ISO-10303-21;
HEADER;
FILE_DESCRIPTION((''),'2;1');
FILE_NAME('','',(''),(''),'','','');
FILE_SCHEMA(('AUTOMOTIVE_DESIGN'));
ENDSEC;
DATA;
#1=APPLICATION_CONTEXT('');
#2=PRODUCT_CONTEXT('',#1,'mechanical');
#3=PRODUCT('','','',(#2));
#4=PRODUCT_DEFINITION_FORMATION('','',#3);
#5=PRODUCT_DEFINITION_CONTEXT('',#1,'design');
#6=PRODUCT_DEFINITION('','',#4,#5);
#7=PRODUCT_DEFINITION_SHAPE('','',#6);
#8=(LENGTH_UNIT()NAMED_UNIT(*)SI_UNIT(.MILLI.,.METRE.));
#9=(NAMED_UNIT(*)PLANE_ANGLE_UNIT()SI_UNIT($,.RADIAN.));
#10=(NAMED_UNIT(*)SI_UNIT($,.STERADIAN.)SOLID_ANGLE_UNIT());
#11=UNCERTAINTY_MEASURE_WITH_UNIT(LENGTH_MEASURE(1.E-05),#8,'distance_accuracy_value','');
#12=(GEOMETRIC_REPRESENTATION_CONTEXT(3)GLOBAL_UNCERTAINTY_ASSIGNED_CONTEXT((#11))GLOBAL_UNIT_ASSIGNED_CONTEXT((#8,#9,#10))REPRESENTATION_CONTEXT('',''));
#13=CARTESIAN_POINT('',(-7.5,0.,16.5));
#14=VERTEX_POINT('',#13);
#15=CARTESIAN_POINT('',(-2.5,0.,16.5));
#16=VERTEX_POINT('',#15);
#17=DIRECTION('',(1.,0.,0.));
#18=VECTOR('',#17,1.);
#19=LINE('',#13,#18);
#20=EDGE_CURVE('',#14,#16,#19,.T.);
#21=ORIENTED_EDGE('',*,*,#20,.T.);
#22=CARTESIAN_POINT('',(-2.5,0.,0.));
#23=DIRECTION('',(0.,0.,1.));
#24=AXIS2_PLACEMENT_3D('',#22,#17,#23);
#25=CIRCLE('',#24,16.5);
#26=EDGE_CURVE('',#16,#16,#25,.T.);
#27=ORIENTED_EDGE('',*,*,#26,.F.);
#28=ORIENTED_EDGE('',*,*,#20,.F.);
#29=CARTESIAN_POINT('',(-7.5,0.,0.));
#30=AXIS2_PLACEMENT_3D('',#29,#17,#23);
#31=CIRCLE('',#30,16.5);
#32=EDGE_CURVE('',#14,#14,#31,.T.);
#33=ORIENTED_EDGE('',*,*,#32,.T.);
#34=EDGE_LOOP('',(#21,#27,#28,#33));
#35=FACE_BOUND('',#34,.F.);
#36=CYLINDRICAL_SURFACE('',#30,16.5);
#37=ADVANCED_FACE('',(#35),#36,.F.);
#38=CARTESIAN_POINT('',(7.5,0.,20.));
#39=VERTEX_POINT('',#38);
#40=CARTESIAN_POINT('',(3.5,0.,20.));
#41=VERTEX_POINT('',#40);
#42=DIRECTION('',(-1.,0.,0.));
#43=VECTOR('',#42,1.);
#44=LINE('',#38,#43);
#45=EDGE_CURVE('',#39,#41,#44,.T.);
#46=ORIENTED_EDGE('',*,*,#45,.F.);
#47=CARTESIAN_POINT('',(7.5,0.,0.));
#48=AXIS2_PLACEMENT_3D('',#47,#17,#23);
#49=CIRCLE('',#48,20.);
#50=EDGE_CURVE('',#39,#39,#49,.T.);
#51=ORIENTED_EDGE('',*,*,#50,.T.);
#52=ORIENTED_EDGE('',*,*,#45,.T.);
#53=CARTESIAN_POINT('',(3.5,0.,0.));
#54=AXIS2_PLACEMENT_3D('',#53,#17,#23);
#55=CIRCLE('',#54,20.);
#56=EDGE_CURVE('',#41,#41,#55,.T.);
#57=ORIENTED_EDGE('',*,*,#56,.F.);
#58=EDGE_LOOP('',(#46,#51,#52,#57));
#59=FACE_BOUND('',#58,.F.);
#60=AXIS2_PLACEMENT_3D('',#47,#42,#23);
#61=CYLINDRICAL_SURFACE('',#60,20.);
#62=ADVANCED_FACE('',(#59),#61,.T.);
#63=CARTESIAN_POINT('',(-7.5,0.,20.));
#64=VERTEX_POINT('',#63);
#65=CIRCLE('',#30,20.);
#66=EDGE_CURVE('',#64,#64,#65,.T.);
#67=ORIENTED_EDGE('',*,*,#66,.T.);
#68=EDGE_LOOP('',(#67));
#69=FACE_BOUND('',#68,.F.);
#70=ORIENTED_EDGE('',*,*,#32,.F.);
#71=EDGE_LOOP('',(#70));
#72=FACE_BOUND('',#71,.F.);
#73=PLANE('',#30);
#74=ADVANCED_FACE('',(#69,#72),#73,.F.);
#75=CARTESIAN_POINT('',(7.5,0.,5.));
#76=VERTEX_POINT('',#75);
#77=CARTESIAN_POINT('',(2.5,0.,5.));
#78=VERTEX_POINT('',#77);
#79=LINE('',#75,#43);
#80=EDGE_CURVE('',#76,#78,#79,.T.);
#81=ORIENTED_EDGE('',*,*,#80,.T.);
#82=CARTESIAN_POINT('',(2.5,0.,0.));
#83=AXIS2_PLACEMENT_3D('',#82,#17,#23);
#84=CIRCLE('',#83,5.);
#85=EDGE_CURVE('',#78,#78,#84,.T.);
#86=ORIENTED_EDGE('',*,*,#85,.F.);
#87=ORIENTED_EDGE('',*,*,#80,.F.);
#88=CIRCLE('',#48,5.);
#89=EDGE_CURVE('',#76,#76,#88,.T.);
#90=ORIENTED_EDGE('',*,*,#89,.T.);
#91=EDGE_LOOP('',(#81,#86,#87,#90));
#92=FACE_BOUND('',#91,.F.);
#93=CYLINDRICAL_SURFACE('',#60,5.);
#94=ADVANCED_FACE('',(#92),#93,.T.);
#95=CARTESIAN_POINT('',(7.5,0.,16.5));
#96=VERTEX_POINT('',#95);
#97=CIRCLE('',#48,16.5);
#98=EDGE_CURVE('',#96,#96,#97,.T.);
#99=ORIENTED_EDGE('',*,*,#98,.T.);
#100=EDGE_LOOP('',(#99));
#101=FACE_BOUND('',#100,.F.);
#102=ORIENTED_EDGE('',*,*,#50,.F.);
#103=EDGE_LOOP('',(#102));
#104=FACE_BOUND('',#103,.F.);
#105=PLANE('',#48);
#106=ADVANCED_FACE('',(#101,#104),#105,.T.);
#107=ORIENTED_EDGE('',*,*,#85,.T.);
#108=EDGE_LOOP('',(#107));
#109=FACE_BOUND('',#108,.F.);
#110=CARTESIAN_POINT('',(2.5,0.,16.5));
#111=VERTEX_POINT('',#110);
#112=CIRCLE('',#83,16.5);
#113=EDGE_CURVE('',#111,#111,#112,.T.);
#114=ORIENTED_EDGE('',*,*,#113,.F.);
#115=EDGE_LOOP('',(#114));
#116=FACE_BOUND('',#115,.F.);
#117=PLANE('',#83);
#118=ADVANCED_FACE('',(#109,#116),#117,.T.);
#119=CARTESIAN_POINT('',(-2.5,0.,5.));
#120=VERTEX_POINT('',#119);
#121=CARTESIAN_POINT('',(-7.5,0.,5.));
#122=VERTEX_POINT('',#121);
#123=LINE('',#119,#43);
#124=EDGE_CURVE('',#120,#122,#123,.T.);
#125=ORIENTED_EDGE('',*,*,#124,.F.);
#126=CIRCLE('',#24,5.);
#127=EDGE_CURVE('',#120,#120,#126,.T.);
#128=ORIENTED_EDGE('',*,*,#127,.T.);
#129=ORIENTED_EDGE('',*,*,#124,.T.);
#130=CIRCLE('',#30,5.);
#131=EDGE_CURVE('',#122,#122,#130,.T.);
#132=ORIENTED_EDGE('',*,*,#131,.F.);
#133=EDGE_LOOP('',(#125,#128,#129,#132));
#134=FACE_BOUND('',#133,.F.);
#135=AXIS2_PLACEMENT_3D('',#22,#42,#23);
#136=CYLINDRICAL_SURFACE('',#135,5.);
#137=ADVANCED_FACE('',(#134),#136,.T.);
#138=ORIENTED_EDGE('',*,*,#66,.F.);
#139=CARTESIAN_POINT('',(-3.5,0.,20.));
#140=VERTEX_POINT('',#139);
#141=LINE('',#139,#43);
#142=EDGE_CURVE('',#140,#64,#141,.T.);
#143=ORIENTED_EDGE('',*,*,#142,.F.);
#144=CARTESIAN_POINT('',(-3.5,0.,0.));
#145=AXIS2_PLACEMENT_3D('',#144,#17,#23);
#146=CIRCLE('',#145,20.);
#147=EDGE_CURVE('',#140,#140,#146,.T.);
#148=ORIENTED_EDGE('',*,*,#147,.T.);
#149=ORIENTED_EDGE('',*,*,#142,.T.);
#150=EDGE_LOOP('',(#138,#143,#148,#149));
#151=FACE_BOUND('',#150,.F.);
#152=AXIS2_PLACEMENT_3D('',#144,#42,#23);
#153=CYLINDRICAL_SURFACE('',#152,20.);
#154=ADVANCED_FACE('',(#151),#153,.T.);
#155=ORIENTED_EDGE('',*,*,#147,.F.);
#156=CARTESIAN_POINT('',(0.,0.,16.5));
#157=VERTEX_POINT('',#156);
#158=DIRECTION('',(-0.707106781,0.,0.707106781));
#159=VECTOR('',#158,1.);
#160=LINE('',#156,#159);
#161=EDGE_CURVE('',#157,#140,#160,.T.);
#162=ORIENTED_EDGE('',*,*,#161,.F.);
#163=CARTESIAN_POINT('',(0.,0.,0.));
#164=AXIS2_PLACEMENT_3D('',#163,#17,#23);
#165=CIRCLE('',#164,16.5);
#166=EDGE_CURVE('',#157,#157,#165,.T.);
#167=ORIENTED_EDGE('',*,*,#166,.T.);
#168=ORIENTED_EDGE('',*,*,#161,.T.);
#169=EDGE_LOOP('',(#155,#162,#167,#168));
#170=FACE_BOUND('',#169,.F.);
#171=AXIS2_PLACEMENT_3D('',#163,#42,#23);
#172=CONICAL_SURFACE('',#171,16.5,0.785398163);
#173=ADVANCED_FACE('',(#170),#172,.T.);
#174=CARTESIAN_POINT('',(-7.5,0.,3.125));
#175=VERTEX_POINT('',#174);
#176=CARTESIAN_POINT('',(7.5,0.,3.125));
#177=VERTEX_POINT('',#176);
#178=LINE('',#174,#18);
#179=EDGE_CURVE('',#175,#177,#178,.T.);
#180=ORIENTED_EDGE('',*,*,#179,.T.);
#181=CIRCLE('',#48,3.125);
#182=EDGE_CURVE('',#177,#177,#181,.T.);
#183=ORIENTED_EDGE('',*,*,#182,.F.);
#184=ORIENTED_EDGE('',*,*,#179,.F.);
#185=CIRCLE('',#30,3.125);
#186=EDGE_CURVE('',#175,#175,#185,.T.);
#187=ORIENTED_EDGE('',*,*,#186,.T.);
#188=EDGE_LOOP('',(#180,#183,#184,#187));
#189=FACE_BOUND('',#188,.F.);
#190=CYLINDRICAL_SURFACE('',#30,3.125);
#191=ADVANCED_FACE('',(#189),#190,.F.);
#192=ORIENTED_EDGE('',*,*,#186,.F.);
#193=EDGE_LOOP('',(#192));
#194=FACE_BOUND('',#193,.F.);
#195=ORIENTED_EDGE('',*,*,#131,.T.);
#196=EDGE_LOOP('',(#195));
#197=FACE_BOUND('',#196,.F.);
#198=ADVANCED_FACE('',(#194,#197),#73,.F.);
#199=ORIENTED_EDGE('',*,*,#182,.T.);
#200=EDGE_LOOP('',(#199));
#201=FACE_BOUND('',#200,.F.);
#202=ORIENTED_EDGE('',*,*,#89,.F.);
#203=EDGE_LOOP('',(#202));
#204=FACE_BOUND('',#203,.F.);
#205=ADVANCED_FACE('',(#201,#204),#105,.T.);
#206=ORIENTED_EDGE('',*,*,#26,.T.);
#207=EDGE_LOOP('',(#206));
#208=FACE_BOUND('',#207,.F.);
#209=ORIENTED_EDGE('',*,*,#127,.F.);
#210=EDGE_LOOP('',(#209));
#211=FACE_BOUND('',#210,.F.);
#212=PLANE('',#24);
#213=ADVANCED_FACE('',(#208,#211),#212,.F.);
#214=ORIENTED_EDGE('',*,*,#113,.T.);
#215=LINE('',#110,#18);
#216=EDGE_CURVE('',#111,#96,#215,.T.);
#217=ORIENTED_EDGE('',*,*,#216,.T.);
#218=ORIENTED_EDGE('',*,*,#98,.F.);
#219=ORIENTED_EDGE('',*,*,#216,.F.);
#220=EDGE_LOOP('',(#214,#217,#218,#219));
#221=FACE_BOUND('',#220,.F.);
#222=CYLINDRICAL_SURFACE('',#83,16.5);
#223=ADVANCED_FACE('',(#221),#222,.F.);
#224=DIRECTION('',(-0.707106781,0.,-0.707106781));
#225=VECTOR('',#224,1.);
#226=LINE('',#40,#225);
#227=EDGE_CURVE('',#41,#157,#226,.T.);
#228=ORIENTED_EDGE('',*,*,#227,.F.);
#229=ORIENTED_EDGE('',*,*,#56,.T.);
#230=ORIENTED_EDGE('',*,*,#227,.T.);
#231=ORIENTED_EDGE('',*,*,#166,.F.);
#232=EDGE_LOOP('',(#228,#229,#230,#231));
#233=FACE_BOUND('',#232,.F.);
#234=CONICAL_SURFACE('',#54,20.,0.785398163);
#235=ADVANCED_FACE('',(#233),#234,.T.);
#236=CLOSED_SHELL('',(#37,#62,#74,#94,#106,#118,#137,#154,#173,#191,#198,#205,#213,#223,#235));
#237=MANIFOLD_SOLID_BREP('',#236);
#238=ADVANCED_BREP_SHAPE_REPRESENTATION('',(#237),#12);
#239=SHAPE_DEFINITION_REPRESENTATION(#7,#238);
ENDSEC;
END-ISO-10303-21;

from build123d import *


with BuildPart() as part:
    # Sketch1 → Revolve1 (revolve)
    with BuildSketch(Plane.XY, mode=Mode.PRIVATE) as revolve1_sk:
        Polygon((3.5, 20), (0, 16.5), (-3.5, 20), (-7.5, 20), (-7.5, 16.5), (-2.5, 16.5), (-2.5, 5), (-7.5, 5), (-7.5, 3.125), (7.5, 3.125), (7.5, 5), (2.5, 5), (2.5, 16.5), (7.5, 16.5), (7.5, 20), align=None)
    revolve(revolve1_sk.sketch.rotate(Axis((-45.5, 0, 0), (1, 0, 0)), 90), axis=Axis((-45.5, 0, 0), (1, 0, 0)))


solid = part.part
